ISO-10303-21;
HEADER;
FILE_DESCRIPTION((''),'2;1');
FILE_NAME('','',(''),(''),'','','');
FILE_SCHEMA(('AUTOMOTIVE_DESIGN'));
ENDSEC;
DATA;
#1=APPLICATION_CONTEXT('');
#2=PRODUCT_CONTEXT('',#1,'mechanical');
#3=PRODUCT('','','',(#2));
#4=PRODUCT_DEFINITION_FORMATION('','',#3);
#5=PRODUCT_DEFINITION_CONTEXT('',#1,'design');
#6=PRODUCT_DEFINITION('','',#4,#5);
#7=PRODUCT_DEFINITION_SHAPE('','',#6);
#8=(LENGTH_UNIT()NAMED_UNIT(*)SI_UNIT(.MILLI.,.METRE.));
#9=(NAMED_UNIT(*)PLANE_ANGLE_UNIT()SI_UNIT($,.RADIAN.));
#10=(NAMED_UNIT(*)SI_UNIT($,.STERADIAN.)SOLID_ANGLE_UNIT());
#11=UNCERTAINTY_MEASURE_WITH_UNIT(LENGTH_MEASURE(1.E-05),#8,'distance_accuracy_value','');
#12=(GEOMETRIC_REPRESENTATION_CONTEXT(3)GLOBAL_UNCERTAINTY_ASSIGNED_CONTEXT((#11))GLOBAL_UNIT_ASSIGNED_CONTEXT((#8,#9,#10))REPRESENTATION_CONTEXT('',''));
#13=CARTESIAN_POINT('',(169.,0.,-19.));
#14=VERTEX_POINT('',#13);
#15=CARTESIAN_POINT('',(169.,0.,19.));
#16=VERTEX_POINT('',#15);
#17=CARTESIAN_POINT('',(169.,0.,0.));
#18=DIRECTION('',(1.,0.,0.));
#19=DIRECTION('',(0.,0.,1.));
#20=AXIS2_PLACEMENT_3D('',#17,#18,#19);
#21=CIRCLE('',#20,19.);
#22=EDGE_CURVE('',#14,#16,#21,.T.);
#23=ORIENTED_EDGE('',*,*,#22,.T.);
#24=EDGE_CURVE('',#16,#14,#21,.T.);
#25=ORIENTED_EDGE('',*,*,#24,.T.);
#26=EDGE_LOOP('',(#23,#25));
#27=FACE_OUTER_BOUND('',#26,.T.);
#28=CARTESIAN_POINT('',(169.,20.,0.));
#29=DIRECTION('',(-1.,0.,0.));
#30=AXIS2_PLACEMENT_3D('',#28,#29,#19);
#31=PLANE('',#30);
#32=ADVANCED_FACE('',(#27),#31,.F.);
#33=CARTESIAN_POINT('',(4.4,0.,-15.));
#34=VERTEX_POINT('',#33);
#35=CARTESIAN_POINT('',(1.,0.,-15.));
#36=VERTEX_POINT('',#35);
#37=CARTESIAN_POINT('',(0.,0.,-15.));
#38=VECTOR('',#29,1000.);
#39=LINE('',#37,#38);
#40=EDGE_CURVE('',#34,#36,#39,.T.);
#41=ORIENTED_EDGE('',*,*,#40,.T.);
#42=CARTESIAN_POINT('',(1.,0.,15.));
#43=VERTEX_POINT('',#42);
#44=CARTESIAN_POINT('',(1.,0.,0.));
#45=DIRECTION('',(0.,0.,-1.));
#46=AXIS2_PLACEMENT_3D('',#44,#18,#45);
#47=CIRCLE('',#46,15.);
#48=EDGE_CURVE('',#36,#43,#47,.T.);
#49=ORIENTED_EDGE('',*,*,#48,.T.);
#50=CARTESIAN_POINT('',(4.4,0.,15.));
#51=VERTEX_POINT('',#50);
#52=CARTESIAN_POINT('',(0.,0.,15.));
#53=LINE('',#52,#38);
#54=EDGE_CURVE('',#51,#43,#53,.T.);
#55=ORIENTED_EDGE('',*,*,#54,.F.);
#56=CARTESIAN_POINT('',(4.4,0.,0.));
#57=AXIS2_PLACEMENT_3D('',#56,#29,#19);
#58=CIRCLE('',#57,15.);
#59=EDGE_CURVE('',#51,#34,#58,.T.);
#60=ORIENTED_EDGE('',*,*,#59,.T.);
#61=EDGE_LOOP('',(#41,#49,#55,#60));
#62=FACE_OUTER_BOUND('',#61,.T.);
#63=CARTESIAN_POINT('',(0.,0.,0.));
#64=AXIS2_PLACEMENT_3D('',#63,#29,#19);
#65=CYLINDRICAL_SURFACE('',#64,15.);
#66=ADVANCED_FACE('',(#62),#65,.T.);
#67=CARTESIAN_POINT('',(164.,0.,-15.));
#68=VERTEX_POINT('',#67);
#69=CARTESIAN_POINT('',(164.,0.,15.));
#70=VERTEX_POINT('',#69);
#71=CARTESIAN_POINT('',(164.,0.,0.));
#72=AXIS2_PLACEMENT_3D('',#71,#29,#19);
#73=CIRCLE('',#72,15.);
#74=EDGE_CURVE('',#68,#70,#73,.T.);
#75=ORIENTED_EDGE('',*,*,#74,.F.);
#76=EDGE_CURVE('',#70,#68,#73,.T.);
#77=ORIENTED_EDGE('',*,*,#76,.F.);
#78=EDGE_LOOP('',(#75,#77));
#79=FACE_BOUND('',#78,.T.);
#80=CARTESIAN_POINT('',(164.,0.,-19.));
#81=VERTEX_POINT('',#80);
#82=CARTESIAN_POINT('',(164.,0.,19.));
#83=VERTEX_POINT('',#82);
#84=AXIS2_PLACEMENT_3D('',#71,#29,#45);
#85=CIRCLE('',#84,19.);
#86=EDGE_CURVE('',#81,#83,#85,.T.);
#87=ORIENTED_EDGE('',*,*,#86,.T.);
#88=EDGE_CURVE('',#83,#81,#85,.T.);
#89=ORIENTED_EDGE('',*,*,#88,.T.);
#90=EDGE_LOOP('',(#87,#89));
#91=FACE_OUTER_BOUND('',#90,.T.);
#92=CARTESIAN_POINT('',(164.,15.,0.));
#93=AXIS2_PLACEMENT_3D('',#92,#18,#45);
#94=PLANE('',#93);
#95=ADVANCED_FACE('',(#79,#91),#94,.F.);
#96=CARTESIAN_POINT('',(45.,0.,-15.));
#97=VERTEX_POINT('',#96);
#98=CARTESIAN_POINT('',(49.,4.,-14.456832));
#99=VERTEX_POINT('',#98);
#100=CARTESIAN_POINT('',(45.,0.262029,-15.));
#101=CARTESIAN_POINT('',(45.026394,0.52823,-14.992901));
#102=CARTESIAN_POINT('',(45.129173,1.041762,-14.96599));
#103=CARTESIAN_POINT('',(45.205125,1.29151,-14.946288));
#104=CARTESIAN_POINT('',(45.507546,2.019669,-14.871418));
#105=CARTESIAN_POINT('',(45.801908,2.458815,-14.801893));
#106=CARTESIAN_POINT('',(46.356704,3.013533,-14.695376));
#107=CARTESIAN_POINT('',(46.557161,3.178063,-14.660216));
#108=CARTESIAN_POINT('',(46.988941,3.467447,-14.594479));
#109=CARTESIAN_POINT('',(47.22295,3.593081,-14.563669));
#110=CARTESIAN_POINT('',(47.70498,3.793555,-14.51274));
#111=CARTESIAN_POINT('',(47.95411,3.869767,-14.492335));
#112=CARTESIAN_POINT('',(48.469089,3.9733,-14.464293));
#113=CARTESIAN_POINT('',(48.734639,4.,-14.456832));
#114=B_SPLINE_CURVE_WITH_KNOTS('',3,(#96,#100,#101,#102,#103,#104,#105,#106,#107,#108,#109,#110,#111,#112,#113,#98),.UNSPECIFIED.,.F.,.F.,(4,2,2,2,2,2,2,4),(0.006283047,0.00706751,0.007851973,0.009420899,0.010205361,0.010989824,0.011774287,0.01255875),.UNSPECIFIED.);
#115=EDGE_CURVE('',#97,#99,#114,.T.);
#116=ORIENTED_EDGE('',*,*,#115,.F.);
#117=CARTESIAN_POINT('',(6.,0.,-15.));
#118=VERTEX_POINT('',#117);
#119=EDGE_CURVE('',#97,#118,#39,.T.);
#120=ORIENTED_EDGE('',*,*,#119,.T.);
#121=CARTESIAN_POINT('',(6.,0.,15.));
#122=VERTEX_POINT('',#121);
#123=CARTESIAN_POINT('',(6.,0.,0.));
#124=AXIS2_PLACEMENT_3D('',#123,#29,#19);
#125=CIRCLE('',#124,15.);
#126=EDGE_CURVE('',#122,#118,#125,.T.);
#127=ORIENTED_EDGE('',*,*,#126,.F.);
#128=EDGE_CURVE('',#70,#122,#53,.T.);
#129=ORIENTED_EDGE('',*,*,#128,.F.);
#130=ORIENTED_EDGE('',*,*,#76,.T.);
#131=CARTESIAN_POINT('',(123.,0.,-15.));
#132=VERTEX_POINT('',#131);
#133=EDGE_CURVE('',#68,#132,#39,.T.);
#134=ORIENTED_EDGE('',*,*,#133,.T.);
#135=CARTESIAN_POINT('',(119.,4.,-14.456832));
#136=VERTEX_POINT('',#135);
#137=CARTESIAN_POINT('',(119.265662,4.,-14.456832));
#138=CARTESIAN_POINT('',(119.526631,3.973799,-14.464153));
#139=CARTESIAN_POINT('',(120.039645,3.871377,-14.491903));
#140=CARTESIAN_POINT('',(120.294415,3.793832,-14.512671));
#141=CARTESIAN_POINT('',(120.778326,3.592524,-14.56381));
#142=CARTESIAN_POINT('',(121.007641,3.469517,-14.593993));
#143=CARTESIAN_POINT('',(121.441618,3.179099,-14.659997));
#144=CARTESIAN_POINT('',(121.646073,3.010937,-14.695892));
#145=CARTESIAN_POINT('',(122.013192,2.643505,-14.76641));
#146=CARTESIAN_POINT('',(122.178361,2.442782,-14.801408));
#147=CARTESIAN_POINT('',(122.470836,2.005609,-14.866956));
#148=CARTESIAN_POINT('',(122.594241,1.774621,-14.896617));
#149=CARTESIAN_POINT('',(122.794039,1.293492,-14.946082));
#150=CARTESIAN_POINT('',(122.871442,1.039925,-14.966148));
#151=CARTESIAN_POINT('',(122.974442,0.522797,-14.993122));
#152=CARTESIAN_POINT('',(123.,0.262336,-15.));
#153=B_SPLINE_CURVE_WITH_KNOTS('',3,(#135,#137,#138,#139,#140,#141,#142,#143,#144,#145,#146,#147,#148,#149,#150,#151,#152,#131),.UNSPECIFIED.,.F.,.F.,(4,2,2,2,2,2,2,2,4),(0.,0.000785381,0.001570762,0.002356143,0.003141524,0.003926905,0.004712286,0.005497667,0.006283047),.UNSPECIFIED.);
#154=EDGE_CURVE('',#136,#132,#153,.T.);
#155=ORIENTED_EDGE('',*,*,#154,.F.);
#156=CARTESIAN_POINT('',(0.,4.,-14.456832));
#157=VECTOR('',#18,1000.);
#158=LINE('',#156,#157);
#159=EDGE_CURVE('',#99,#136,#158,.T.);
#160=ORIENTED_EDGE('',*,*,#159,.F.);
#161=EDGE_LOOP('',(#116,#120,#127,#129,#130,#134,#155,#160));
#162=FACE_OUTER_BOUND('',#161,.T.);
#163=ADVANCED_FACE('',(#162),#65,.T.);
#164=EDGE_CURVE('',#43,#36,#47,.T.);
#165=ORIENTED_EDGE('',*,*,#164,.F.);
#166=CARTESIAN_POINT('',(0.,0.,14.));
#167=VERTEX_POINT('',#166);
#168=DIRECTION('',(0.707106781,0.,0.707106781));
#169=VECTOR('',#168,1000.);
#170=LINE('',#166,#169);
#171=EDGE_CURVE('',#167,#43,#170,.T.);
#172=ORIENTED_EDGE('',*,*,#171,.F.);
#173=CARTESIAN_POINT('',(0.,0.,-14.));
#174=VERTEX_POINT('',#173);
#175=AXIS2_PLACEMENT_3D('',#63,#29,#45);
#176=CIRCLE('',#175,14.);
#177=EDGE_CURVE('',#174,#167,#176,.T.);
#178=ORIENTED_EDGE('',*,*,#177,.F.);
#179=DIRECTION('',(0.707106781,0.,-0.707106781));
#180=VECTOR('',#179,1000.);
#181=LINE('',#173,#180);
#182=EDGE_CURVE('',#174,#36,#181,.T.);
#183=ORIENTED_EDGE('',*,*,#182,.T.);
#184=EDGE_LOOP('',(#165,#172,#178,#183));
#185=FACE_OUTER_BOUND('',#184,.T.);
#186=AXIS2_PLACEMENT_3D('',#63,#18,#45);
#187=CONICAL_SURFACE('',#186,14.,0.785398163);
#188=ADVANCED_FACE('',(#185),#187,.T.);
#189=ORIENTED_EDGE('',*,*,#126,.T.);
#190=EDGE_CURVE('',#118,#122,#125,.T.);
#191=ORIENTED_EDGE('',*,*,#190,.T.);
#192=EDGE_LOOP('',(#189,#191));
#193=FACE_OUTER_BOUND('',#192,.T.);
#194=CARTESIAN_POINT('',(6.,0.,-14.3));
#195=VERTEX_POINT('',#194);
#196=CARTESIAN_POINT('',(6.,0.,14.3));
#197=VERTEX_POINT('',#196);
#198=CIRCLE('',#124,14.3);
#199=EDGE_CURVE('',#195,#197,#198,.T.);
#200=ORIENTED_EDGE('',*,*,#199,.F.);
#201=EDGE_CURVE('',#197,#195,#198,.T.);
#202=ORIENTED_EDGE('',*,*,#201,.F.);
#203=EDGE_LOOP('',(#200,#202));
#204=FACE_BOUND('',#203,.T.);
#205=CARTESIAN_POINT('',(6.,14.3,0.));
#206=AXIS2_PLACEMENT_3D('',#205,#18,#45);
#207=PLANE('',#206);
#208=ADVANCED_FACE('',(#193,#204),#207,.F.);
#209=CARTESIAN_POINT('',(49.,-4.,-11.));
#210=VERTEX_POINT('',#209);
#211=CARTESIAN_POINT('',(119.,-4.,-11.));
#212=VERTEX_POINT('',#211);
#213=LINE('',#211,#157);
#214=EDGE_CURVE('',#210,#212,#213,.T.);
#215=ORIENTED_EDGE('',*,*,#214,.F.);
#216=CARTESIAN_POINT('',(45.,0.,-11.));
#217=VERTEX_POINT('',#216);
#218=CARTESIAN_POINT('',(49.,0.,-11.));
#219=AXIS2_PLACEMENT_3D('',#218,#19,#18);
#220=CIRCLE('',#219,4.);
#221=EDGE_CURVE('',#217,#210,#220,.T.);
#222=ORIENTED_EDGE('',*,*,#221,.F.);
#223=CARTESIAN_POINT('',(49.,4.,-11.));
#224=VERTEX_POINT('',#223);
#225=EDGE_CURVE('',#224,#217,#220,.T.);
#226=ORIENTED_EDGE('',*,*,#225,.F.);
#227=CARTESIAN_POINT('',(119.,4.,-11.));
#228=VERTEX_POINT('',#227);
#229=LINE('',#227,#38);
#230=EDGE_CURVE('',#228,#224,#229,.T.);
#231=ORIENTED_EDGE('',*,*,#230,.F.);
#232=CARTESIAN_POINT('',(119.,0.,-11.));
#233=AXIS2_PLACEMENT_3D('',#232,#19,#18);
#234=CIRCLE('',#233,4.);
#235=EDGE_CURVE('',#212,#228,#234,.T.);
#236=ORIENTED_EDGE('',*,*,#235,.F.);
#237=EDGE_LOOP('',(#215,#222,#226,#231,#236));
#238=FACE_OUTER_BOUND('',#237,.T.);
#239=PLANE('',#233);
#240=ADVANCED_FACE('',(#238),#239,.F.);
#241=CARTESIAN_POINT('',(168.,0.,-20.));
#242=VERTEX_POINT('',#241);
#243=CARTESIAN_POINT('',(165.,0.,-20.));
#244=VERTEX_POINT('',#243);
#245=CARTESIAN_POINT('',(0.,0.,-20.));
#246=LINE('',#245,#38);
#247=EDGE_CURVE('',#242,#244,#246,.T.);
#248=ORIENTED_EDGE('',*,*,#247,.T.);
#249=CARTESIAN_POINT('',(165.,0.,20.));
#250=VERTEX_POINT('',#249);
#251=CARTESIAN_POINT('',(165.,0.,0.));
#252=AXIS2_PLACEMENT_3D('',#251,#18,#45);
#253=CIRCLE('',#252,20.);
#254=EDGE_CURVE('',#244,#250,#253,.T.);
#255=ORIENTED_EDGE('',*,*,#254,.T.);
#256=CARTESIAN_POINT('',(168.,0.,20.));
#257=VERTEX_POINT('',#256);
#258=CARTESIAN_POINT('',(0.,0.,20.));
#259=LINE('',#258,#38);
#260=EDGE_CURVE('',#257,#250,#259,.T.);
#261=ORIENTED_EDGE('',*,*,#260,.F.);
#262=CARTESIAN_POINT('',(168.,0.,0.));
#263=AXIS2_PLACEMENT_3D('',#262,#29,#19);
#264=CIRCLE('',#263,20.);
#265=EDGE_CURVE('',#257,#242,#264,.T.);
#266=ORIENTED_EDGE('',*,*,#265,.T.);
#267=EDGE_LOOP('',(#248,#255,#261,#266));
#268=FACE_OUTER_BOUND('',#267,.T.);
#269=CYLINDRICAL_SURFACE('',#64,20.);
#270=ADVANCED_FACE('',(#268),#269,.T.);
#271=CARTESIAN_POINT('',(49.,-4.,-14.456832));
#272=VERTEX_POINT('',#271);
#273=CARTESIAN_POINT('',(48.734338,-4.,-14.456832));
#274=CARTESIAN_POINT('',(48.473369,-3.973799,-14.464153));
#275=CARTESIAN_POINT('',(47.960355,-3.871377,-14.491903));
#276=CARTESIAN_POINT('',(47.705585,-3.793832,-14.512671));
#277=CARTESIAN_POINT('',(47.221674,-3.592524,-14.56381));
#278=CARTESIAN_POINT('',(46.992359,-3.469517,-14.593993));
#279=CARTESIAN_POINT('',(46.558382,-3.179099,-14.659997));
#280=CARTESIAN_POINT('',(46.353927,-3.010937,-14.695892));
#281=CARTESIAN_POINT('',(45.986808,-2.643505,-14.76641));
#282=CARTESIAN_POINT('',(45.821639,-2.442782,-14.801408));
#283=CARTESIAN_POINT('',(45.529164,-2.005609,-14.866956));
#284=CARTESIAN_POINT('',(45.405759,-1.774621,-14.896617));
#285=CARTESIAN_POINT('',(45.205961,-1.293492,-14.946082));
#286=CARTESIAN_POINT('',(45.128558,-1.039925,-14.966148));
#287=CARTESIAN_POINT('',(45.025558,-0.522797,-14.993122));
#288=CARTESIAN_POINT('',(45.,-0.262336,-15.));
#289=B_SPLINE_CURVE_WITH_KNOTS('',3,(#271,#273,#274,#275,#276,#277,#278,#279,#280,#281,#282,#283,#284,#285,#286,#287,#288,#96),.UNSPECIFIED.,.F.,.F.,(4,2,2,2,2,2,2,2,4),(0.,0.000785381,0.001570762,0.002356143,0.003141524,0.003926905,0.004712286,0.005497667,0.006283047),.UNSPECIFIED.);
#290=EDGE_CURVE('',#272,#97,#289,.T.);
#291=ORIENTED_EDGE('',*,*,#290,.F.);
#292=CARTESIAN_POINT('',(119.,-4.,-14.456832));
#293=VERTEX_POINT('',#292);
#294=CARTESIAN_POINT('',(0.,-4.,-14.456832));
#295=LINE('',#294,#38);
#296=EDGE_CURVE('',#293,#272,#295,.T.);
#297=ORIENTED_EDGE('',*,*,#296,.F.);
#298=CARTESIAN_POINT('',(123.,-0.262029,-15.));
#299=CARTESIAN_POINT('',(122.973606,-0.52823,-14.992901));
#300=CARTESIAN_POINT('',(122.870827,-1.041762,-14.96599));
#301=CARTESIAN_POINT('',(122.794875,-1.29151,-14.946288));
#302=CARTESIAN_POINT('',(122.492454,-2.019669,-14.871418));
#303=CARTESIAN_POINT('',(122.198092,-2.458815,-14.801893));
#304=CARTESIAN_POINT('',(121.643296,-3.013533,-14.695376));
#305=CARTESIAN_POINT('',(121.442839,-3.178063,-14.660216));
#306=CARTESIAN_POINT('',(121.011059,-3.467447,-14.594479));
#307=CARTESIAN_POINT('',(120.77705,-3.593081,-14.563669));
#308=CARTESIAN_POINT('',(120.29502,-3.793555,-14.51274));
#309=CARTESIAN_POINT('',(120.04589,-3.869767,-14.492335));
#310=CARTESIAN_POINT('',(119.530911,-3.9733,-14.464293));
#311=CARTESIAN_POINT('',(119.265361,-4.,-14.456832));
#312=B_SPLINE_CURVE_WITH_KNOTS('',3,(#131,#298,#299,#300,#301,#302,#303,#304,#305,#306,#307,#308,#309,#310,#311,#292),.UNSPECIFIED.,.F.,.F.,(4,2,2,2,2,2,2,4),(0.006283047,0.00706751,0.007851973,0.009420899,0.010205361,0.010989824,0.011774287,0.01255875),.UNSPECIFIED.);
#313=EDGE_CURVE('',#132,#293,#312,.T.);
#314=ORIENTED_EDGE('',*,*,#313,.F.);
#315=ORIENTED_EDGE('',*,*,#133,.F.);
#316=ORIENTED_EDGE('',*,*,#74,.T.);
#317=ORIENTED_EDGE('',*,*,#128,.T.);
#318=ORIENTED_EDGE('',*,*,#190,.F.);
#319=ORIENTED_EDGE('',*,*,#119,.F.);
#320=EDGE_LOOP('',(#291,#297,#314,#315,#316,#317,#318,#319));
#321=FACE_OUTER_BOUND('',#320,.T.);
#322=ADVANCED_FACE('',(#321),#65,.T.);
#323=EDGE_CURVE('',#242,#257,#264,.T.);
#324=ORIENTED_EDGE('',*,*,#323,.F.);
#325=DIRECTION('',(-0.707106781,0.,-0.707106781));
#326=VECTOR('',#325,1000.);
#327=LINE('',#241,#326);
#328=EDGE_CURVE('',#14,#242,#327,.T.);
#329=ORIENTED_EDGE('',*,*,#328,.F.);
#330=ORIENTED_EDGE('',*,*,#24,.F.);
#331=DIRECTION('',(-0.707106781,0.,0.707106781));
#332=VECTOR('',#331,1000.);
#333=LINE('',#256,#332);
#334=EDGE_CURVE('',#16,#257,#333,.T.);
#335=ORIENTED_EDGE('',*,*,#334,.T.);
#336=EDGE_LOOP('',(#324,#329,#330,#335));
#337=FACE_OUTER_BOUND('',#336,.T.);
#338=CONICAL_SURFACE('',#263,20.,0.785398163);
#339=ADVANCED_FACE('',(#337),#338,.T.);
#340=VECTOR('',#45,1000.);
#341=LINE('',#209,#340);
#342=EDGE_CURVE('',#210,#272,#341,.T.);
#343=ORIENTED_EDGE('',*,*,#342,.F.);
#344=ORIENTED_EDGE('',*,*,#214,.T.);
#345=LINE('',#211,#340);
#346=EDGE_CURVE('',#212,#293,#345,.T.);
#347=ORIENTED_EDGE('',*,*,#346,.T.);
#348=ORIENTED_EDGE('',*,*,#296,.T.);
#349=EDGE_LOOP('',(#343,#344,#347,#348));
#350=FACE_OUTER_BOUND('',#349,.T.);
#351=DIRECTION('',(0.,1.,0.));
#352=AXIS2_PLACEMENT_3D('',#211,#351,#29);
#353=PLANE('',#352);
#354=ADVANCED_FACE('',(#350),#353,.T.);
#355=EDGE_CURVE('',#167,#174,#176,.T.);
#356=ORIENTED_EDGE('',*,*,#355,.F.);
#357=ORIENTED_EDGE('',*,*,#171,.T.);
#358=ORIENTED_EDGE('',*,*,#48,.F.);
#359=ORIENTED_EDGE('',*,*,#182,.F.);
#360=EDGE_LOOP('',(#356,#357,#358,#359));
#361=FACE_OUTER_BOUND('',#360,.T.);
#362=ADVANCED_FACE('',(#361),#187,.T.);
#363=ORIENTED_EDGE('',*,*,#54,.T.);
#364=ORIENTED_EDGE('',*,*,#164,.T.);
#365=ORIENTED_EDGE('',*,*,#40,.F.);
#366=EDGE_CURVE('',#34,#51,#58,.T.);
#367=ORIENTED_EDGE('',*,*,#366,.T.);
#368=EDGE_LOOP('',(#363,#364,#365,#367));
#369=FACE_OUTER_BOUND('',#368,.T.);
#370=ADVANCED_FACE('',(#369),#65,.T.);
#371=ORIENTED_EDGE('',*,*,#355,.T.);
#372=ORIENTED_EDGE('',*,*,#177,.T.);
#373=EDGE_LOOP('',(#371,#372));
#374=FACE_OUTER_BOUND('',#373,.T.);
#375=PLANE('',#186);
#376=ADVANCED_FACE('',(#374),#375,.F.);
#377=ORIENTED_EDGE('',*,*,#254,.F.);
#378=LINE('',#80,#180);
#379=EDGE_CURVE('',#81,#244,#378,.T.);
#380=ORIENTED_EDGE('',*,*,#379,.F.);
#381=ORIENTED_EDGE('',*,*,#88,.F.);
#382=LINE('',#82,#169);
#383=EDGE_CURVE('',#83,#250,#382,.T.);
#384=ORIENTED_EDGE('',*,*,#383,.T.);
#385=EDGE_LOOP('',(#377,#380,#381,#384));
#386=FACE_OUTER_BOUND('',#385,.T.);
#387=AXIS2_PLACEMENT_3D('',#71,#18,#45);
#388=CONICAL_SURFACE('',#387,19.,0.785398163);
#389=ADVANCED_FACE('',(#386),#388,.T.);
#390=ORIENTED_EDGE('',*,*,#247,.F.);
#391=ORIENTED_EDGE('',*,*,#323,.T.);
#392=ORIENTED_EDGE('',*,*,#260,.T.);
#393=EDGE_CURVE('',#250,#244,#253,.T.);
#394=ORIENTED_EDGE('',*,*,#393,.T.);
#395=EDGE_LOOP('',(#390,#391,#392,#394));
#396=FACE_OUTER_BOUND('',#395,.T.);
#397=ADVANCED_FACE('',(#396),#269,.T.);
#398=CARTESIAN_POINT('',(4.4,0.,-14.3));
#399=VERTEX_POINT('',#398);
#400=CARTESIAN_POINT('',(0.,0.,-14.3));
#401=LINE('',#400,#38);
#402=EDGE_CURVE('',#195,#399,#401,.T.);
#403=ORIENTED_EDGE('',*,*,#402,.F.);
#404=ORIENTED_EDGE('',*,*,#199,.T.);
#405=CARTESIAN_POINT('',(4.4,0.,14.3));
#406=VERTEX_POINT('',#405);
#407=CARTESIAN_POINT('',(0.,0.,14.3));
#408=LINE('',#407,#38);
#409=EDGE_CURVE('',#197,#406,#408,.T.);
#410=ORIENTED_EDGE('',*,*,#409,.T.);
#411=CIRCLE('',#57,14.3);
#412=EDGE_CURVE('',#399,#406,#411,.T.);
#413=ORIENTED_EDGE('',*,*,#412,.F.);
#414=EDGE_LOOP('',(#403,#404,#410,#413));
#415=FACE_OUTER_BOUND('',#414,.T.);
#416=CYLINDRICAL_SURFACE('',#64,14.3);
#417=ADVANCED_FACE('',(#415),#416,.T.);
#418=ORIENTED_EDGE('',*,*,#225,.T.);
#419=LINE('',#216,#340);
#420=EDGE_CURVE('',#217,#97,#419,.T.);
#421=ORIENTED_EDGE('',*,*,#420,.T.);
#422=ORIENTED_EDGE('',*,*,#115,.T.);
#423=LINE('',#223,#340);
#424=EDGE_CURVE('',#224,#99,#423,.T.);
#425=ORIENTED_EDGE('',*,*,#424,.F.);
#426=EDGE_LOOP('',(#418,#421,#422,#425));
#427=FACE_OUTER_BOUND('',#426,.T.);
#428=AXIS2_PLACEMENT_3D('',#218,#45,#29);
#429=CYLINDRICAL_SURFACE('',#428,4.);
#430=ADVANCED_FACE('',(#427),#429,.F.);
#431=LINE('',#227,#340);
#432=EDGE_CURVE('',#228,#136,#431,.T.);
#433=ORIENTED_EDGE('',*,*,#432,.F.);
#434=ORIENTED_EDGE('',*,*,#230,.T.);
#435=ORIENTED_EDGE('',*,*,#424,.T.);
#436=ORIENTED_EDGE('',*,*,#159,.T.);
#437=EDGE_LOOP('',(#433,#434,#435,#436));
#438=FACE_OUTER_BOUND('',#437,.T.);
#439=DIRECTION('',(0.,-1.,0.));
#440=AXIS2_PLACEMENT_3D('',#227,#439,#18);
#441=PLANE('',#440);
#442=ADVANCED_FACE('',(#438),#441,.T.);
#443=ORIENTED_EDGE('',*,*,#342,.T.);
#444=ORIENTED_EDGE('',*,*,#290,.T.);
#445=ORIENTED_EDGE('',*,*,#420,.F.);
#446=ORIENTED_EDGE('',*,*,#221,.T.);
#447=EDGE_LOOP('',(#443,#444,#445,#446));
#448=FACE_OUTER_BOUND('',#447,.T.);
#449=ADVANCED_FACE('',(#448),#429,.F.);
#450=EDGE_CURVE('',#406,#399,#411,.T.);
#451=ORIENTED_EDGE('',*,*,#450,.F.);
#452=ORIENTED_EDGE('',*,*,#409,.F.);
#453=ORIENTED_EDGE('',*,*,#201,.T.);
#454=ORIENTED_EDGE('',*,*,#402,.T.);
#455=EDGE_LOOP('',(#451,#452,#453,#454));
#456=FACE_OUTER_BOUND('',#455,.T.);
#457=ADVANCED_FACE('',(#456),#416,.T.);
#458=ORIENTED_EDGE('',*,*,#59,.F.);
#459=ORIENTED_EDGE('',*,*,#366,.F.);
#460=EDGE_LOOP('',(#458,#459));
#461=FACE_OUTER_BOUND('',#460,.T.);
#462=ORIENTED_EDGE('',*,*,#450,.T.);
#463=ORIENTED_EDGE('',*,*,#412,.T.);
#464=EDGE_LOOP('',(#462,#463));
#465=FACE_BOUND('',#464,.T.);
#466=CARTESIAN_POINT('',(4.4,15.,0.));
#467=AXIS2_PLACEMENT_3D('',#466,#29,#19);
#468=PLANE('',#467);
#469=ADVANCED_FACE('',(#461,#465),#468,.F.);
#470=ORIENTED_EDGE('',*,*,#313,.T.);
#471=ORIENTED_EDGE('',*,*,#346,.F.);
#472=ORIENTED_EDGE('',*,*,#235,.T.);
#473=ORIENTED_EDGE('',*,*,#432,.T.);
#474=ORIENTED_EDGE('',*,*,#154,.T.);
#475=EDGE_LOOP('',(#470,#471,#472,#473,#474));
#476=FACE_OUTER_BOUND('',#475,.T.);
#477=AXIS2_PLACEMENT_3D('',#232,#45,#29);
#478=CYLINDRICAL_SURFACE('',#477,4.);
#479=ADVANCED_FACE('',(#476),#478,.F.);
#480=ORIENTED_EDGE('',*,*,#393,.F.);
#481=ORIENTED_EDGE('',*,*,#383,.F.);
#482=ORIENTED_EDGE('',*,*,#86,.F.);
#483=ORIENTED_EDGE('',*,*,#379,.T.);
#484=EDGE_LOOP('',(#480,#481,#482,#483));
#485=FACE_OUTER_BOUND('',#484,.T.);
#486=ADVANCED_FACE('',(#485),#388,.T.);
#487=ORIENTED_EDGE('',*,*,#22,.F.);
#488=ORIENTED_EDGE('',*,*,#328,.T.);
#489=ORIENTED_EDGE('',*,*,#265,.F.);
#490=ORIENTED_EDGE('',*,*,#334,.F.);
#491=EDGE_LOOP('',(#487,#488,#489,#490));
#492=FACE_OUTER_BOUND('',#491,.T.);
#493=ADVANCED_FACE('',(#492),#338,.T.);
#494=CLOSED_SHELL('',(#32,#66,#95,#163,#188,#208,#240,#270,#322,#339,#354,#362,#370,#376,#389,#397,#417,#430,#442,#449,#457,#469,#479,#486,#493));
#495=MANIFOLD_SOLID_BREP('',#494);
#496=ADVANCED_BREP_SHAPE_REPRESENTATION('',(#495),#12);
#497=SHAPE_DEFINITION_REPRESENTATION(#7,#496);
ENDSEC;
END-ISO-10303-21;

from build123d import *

# Parameters (mm, degrees)
CUT_EXTRUDE_START   = -15
CUT_EXTRUDE_1_DEPTH = 4
CHAMFER_1_SIZE      = 1


with BuildPart() as part:
    # 草图1 → 旋转1 (revolve)
    with BuildSketch(Plane.XY, mode=Mode.PRIVATE) as revolve_1_sk:
        Polygon((0, 0), (0, 15), (4.4, 15), (4.4, 14.3), (6, 14.3), (6, 15), (164, 15), (164, 20), (169, 20), (169, 0), align=None)
    revolve(revolve_1_sk.sketch.rotate(Axis((0, 0, 0), (1, 0, 0)), 90), axis=Axis((0, 0, 0), (1, 0, 0)))

    # 草图2 → 切除-拉伸1 (cut)
    with BuildSketch(Plane.XY.offset(CUT_EXTRUDE_START)):
        with BuildLine():
            Line((119, -4), (49, -4))
            ThreePointArc((49, -4), (45, 0), (49, 4))
            Line((49, 4), (119, 4))
            ThreePointArc((119, 4), (123, 0), (119, -4))
        make_face()
    extrude(amount=CUT_EXTRUDE_1_DEPTH, mode=Mode.SUBTRACT)

    # 倒角1
    chamfer_1_edges = [part.edges().sort_by_distance(p)[0] for p in [
        (0, 0, -15),
        (169, 0, -20),
        (164, 0, -20),
    ]]
    chamfer(chamfer_1_edges, length=CHAMFER_1_SIZE)


solid = part.part
